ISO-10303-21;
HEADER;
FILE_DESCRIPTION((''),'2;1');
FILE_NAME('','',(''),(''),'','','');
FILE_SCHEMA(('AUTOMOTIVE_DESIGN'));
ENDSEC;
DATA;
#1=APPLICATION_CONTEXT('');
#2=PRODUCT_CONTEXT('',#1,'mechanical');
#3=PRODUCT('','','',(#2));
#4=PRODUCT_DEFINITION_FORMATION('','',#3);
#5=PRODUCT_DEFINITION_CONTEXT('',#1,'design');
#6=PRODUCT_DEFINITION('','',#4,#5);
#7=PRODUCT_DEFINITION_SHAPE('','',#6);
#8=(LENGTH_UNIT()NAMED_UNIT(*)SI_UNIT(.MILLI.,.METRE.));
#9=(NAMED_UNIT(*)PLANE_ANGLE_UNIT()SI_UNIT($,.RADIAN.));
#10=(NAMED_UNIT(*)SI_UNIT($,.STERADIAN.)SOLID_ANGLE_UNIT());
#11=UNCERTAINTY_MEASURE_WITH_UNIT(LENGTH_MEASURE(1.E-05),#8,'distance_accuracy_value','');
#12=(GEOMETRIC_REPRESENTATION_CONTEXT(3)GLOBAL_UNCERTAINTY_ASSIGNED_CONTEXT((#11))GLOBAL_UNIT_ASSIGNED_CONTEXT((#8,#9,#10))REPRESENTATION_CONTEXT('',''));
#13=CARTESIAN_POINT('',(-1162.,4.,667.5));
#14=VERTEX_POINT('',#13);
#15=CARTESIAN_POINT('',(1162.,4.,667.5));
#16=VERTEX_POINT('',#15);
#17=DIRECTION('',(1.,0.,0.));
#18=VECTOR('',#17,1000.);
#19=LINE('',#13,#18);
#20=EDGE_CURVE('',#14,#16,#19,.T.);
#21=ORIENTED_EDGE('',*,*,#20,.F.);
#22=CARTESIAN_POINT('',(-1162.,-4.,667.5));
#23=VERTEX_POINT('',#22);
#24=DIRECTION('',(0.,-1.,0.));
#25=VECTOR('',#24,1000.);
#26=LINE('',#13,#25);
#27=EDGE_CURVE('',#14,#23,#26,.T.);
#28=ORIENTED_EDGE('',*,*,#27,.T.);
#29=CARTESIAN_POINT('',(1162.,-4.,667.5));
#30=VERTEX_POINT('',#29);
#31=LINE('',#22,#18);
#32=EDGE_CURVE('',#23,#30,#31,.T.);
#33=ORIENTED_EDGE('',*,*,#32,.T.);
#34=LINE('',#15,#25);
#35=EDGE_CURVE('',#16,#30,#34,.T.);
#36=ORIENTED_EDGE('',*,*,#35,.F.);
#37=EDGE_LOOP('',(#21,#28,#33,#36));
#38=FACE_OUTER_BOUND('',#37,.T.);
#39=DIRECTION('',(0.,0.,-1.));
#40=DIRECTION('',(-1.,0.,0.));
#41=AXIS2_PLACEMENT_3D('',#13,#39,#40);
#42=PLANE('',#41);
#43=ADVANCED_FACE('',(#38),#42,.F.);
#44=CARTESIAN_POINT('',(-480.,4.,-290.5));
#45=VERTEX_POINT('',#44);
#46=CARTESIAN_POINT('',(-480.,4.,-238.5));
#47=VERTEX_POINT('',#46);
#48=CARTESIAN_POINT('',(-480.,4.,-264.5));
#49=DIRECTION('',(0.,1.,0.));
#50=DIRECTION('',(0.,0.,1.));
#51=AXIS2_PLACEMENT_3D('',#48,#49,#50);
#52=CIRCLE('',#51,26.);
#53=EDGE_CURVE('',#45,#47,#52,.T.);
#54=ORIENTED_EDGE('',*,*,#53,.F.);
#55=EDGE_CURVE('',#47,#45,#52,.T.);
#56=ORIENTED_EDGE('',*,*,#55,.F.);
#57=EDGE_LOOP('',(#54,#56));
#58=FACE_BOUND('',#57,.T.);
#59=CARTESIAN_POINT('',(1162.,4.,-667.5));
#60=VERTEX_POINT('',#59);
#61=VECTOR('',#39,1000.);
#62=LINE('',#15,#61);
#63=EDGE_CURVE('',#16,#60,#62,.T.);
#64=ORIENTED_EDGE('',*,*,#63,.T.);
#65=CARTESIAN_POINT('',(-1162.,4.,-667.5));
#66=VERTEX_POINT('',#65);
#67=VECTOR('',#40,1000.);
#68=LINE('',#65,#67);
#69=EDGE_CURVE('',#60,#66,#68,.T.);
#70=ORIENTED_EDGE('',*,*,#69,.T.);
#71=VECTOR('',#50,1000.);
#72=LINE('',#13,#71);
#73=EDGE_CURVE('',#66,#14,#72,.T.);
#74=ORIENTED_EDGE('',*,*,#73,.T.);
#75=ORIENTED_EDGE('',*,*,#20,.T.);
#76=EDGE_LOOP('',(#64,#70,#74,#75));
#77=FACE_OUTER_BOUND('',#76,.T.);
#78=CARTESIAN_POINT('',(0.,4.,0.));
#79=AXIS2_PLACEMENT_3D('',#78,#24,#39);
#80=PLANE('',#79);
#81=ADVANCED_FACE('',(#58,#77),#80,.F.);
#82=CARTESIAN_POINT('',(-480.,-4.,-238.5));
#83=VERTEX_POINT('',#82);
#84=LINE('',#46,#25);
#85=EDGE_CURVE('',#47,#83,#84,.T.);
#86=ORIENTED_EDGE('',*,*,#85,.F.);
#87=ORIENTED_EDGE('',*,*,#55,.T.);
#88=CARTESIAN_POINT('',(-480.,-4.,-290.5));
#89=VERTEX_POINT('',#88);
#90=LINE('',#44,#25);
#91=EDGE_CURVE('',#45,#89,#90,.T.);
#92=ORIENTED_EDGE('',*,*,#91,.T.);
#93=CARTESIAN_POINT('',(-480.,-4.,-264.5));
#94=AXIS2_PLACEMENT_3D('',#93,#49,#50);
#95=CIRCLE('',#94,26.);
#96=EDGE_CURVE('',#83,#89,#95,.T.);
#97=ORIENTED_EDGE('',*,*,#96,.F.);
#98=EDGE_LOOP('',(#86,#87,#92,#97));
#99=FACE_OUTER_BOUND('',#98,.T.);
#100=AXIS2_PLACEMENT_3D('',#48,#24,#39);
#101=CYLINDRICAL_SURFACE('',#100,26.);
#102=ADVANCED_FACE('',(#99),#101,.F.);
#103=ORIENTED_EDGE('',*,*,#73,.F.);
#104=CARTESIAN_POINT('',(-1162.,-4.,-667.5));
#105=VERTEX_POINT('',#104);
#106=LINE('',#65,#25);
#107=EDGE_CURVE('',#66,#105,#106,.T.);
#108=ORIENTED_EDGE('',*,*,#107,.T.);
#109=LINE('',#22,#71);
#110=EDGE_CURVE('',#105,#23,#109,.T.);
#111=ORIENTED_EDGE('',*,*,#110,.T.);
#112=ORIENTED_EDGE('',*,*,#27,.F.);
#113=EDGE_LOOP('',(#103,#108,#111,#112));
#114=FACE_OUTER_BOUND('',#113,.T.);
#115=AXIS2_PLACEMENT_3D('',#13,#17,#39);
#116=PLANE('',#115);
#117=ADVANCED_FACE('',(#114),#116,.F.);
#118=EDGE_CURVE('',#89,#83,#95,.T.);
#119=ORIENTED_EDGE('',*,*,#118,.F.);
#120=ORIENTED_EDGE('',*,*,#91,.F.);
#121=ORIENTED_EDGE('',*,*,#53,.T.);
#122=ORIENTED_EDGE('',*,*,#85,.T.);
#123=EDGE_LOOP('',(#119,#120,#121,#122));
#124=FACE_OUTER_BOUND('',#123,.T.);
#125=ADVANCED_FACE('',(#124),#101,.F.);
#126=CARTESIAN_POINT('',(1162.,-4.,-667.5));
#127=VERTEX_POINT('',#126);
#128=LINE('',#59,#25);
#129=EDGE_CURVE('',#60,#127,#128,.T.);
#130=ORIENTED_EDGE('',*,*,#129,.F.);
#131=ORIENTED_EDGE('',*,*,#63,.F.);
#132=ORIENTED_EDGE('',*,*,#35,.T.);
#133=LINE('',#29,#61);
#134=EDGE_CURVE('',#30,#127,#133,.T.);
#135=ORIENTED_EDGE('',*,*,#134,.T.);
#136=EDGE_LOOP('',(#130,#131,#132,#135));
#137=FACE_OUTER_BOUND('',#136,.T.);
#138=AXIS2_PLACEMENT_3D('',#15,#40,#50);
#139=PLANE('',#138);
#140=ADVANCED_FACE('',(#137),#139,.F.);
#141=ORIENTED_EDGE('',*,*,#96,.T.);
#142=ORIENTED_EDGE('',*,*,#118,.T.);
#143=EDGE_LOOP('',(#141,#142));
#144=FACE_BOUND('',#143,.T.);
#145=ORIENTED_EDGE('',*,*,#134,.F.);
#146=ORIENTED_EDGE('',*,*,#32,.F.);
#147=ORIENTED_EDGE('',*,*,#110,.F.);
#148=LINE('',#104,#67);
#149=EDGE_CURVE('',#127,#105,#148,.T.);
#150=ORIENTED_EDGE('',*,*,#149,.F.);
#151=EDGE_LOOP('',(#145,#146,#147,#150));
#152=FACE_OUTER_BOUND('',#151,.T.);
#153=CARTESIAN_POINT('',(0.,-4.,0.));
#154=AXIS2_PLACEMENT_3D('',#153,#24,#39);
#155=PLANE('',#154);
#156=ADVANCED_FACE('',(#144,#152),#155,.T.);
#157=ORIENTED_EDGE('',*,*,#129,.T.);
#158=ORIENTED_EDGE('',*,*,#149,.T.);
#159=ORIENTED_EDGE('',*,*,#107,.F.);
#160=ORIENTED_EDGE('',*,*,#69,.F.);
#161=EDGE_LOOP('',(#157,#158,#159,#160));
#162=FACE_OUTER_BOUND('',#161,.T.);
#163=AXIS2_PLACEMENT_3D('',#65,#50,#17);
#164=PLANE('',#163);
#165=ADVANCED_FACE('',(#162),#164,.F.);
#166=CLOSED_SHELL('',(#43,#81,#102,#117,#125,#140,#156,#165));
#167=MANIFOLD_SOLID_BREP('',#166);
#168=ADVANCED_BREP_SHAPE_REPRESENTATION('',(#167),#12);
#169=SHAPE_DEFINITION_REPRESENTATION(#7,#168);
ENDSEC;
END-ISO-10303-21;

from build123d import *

# Parameters (mm, degrees)
SKETCH_1_W      = 2324
SKETCH_1_H      = 1335
SKETCH_1_R      = 26
EXTRUDE_1_DEPTH = 4


with BuildPart() as part:
    # 草图1 → 凸台-拉伸1 (new, symmetric)
    with BuildSketch(Plane(origin=(0, 0, 0), x_dir=(1, 0, 0), z_dir=(0, 1, 0))):
        Rectangle(SKETCH_1_W, SKETCH_1_H)
        with Locations(Location((-480, 264.5, 0), (0, 0, 270))):
            Circle(SKETCH_1_R, mode=Mode.SUBTRACT)
    extrude(amount=EXTRUDE_1_DEPTH, both=True)


solid = part.part
